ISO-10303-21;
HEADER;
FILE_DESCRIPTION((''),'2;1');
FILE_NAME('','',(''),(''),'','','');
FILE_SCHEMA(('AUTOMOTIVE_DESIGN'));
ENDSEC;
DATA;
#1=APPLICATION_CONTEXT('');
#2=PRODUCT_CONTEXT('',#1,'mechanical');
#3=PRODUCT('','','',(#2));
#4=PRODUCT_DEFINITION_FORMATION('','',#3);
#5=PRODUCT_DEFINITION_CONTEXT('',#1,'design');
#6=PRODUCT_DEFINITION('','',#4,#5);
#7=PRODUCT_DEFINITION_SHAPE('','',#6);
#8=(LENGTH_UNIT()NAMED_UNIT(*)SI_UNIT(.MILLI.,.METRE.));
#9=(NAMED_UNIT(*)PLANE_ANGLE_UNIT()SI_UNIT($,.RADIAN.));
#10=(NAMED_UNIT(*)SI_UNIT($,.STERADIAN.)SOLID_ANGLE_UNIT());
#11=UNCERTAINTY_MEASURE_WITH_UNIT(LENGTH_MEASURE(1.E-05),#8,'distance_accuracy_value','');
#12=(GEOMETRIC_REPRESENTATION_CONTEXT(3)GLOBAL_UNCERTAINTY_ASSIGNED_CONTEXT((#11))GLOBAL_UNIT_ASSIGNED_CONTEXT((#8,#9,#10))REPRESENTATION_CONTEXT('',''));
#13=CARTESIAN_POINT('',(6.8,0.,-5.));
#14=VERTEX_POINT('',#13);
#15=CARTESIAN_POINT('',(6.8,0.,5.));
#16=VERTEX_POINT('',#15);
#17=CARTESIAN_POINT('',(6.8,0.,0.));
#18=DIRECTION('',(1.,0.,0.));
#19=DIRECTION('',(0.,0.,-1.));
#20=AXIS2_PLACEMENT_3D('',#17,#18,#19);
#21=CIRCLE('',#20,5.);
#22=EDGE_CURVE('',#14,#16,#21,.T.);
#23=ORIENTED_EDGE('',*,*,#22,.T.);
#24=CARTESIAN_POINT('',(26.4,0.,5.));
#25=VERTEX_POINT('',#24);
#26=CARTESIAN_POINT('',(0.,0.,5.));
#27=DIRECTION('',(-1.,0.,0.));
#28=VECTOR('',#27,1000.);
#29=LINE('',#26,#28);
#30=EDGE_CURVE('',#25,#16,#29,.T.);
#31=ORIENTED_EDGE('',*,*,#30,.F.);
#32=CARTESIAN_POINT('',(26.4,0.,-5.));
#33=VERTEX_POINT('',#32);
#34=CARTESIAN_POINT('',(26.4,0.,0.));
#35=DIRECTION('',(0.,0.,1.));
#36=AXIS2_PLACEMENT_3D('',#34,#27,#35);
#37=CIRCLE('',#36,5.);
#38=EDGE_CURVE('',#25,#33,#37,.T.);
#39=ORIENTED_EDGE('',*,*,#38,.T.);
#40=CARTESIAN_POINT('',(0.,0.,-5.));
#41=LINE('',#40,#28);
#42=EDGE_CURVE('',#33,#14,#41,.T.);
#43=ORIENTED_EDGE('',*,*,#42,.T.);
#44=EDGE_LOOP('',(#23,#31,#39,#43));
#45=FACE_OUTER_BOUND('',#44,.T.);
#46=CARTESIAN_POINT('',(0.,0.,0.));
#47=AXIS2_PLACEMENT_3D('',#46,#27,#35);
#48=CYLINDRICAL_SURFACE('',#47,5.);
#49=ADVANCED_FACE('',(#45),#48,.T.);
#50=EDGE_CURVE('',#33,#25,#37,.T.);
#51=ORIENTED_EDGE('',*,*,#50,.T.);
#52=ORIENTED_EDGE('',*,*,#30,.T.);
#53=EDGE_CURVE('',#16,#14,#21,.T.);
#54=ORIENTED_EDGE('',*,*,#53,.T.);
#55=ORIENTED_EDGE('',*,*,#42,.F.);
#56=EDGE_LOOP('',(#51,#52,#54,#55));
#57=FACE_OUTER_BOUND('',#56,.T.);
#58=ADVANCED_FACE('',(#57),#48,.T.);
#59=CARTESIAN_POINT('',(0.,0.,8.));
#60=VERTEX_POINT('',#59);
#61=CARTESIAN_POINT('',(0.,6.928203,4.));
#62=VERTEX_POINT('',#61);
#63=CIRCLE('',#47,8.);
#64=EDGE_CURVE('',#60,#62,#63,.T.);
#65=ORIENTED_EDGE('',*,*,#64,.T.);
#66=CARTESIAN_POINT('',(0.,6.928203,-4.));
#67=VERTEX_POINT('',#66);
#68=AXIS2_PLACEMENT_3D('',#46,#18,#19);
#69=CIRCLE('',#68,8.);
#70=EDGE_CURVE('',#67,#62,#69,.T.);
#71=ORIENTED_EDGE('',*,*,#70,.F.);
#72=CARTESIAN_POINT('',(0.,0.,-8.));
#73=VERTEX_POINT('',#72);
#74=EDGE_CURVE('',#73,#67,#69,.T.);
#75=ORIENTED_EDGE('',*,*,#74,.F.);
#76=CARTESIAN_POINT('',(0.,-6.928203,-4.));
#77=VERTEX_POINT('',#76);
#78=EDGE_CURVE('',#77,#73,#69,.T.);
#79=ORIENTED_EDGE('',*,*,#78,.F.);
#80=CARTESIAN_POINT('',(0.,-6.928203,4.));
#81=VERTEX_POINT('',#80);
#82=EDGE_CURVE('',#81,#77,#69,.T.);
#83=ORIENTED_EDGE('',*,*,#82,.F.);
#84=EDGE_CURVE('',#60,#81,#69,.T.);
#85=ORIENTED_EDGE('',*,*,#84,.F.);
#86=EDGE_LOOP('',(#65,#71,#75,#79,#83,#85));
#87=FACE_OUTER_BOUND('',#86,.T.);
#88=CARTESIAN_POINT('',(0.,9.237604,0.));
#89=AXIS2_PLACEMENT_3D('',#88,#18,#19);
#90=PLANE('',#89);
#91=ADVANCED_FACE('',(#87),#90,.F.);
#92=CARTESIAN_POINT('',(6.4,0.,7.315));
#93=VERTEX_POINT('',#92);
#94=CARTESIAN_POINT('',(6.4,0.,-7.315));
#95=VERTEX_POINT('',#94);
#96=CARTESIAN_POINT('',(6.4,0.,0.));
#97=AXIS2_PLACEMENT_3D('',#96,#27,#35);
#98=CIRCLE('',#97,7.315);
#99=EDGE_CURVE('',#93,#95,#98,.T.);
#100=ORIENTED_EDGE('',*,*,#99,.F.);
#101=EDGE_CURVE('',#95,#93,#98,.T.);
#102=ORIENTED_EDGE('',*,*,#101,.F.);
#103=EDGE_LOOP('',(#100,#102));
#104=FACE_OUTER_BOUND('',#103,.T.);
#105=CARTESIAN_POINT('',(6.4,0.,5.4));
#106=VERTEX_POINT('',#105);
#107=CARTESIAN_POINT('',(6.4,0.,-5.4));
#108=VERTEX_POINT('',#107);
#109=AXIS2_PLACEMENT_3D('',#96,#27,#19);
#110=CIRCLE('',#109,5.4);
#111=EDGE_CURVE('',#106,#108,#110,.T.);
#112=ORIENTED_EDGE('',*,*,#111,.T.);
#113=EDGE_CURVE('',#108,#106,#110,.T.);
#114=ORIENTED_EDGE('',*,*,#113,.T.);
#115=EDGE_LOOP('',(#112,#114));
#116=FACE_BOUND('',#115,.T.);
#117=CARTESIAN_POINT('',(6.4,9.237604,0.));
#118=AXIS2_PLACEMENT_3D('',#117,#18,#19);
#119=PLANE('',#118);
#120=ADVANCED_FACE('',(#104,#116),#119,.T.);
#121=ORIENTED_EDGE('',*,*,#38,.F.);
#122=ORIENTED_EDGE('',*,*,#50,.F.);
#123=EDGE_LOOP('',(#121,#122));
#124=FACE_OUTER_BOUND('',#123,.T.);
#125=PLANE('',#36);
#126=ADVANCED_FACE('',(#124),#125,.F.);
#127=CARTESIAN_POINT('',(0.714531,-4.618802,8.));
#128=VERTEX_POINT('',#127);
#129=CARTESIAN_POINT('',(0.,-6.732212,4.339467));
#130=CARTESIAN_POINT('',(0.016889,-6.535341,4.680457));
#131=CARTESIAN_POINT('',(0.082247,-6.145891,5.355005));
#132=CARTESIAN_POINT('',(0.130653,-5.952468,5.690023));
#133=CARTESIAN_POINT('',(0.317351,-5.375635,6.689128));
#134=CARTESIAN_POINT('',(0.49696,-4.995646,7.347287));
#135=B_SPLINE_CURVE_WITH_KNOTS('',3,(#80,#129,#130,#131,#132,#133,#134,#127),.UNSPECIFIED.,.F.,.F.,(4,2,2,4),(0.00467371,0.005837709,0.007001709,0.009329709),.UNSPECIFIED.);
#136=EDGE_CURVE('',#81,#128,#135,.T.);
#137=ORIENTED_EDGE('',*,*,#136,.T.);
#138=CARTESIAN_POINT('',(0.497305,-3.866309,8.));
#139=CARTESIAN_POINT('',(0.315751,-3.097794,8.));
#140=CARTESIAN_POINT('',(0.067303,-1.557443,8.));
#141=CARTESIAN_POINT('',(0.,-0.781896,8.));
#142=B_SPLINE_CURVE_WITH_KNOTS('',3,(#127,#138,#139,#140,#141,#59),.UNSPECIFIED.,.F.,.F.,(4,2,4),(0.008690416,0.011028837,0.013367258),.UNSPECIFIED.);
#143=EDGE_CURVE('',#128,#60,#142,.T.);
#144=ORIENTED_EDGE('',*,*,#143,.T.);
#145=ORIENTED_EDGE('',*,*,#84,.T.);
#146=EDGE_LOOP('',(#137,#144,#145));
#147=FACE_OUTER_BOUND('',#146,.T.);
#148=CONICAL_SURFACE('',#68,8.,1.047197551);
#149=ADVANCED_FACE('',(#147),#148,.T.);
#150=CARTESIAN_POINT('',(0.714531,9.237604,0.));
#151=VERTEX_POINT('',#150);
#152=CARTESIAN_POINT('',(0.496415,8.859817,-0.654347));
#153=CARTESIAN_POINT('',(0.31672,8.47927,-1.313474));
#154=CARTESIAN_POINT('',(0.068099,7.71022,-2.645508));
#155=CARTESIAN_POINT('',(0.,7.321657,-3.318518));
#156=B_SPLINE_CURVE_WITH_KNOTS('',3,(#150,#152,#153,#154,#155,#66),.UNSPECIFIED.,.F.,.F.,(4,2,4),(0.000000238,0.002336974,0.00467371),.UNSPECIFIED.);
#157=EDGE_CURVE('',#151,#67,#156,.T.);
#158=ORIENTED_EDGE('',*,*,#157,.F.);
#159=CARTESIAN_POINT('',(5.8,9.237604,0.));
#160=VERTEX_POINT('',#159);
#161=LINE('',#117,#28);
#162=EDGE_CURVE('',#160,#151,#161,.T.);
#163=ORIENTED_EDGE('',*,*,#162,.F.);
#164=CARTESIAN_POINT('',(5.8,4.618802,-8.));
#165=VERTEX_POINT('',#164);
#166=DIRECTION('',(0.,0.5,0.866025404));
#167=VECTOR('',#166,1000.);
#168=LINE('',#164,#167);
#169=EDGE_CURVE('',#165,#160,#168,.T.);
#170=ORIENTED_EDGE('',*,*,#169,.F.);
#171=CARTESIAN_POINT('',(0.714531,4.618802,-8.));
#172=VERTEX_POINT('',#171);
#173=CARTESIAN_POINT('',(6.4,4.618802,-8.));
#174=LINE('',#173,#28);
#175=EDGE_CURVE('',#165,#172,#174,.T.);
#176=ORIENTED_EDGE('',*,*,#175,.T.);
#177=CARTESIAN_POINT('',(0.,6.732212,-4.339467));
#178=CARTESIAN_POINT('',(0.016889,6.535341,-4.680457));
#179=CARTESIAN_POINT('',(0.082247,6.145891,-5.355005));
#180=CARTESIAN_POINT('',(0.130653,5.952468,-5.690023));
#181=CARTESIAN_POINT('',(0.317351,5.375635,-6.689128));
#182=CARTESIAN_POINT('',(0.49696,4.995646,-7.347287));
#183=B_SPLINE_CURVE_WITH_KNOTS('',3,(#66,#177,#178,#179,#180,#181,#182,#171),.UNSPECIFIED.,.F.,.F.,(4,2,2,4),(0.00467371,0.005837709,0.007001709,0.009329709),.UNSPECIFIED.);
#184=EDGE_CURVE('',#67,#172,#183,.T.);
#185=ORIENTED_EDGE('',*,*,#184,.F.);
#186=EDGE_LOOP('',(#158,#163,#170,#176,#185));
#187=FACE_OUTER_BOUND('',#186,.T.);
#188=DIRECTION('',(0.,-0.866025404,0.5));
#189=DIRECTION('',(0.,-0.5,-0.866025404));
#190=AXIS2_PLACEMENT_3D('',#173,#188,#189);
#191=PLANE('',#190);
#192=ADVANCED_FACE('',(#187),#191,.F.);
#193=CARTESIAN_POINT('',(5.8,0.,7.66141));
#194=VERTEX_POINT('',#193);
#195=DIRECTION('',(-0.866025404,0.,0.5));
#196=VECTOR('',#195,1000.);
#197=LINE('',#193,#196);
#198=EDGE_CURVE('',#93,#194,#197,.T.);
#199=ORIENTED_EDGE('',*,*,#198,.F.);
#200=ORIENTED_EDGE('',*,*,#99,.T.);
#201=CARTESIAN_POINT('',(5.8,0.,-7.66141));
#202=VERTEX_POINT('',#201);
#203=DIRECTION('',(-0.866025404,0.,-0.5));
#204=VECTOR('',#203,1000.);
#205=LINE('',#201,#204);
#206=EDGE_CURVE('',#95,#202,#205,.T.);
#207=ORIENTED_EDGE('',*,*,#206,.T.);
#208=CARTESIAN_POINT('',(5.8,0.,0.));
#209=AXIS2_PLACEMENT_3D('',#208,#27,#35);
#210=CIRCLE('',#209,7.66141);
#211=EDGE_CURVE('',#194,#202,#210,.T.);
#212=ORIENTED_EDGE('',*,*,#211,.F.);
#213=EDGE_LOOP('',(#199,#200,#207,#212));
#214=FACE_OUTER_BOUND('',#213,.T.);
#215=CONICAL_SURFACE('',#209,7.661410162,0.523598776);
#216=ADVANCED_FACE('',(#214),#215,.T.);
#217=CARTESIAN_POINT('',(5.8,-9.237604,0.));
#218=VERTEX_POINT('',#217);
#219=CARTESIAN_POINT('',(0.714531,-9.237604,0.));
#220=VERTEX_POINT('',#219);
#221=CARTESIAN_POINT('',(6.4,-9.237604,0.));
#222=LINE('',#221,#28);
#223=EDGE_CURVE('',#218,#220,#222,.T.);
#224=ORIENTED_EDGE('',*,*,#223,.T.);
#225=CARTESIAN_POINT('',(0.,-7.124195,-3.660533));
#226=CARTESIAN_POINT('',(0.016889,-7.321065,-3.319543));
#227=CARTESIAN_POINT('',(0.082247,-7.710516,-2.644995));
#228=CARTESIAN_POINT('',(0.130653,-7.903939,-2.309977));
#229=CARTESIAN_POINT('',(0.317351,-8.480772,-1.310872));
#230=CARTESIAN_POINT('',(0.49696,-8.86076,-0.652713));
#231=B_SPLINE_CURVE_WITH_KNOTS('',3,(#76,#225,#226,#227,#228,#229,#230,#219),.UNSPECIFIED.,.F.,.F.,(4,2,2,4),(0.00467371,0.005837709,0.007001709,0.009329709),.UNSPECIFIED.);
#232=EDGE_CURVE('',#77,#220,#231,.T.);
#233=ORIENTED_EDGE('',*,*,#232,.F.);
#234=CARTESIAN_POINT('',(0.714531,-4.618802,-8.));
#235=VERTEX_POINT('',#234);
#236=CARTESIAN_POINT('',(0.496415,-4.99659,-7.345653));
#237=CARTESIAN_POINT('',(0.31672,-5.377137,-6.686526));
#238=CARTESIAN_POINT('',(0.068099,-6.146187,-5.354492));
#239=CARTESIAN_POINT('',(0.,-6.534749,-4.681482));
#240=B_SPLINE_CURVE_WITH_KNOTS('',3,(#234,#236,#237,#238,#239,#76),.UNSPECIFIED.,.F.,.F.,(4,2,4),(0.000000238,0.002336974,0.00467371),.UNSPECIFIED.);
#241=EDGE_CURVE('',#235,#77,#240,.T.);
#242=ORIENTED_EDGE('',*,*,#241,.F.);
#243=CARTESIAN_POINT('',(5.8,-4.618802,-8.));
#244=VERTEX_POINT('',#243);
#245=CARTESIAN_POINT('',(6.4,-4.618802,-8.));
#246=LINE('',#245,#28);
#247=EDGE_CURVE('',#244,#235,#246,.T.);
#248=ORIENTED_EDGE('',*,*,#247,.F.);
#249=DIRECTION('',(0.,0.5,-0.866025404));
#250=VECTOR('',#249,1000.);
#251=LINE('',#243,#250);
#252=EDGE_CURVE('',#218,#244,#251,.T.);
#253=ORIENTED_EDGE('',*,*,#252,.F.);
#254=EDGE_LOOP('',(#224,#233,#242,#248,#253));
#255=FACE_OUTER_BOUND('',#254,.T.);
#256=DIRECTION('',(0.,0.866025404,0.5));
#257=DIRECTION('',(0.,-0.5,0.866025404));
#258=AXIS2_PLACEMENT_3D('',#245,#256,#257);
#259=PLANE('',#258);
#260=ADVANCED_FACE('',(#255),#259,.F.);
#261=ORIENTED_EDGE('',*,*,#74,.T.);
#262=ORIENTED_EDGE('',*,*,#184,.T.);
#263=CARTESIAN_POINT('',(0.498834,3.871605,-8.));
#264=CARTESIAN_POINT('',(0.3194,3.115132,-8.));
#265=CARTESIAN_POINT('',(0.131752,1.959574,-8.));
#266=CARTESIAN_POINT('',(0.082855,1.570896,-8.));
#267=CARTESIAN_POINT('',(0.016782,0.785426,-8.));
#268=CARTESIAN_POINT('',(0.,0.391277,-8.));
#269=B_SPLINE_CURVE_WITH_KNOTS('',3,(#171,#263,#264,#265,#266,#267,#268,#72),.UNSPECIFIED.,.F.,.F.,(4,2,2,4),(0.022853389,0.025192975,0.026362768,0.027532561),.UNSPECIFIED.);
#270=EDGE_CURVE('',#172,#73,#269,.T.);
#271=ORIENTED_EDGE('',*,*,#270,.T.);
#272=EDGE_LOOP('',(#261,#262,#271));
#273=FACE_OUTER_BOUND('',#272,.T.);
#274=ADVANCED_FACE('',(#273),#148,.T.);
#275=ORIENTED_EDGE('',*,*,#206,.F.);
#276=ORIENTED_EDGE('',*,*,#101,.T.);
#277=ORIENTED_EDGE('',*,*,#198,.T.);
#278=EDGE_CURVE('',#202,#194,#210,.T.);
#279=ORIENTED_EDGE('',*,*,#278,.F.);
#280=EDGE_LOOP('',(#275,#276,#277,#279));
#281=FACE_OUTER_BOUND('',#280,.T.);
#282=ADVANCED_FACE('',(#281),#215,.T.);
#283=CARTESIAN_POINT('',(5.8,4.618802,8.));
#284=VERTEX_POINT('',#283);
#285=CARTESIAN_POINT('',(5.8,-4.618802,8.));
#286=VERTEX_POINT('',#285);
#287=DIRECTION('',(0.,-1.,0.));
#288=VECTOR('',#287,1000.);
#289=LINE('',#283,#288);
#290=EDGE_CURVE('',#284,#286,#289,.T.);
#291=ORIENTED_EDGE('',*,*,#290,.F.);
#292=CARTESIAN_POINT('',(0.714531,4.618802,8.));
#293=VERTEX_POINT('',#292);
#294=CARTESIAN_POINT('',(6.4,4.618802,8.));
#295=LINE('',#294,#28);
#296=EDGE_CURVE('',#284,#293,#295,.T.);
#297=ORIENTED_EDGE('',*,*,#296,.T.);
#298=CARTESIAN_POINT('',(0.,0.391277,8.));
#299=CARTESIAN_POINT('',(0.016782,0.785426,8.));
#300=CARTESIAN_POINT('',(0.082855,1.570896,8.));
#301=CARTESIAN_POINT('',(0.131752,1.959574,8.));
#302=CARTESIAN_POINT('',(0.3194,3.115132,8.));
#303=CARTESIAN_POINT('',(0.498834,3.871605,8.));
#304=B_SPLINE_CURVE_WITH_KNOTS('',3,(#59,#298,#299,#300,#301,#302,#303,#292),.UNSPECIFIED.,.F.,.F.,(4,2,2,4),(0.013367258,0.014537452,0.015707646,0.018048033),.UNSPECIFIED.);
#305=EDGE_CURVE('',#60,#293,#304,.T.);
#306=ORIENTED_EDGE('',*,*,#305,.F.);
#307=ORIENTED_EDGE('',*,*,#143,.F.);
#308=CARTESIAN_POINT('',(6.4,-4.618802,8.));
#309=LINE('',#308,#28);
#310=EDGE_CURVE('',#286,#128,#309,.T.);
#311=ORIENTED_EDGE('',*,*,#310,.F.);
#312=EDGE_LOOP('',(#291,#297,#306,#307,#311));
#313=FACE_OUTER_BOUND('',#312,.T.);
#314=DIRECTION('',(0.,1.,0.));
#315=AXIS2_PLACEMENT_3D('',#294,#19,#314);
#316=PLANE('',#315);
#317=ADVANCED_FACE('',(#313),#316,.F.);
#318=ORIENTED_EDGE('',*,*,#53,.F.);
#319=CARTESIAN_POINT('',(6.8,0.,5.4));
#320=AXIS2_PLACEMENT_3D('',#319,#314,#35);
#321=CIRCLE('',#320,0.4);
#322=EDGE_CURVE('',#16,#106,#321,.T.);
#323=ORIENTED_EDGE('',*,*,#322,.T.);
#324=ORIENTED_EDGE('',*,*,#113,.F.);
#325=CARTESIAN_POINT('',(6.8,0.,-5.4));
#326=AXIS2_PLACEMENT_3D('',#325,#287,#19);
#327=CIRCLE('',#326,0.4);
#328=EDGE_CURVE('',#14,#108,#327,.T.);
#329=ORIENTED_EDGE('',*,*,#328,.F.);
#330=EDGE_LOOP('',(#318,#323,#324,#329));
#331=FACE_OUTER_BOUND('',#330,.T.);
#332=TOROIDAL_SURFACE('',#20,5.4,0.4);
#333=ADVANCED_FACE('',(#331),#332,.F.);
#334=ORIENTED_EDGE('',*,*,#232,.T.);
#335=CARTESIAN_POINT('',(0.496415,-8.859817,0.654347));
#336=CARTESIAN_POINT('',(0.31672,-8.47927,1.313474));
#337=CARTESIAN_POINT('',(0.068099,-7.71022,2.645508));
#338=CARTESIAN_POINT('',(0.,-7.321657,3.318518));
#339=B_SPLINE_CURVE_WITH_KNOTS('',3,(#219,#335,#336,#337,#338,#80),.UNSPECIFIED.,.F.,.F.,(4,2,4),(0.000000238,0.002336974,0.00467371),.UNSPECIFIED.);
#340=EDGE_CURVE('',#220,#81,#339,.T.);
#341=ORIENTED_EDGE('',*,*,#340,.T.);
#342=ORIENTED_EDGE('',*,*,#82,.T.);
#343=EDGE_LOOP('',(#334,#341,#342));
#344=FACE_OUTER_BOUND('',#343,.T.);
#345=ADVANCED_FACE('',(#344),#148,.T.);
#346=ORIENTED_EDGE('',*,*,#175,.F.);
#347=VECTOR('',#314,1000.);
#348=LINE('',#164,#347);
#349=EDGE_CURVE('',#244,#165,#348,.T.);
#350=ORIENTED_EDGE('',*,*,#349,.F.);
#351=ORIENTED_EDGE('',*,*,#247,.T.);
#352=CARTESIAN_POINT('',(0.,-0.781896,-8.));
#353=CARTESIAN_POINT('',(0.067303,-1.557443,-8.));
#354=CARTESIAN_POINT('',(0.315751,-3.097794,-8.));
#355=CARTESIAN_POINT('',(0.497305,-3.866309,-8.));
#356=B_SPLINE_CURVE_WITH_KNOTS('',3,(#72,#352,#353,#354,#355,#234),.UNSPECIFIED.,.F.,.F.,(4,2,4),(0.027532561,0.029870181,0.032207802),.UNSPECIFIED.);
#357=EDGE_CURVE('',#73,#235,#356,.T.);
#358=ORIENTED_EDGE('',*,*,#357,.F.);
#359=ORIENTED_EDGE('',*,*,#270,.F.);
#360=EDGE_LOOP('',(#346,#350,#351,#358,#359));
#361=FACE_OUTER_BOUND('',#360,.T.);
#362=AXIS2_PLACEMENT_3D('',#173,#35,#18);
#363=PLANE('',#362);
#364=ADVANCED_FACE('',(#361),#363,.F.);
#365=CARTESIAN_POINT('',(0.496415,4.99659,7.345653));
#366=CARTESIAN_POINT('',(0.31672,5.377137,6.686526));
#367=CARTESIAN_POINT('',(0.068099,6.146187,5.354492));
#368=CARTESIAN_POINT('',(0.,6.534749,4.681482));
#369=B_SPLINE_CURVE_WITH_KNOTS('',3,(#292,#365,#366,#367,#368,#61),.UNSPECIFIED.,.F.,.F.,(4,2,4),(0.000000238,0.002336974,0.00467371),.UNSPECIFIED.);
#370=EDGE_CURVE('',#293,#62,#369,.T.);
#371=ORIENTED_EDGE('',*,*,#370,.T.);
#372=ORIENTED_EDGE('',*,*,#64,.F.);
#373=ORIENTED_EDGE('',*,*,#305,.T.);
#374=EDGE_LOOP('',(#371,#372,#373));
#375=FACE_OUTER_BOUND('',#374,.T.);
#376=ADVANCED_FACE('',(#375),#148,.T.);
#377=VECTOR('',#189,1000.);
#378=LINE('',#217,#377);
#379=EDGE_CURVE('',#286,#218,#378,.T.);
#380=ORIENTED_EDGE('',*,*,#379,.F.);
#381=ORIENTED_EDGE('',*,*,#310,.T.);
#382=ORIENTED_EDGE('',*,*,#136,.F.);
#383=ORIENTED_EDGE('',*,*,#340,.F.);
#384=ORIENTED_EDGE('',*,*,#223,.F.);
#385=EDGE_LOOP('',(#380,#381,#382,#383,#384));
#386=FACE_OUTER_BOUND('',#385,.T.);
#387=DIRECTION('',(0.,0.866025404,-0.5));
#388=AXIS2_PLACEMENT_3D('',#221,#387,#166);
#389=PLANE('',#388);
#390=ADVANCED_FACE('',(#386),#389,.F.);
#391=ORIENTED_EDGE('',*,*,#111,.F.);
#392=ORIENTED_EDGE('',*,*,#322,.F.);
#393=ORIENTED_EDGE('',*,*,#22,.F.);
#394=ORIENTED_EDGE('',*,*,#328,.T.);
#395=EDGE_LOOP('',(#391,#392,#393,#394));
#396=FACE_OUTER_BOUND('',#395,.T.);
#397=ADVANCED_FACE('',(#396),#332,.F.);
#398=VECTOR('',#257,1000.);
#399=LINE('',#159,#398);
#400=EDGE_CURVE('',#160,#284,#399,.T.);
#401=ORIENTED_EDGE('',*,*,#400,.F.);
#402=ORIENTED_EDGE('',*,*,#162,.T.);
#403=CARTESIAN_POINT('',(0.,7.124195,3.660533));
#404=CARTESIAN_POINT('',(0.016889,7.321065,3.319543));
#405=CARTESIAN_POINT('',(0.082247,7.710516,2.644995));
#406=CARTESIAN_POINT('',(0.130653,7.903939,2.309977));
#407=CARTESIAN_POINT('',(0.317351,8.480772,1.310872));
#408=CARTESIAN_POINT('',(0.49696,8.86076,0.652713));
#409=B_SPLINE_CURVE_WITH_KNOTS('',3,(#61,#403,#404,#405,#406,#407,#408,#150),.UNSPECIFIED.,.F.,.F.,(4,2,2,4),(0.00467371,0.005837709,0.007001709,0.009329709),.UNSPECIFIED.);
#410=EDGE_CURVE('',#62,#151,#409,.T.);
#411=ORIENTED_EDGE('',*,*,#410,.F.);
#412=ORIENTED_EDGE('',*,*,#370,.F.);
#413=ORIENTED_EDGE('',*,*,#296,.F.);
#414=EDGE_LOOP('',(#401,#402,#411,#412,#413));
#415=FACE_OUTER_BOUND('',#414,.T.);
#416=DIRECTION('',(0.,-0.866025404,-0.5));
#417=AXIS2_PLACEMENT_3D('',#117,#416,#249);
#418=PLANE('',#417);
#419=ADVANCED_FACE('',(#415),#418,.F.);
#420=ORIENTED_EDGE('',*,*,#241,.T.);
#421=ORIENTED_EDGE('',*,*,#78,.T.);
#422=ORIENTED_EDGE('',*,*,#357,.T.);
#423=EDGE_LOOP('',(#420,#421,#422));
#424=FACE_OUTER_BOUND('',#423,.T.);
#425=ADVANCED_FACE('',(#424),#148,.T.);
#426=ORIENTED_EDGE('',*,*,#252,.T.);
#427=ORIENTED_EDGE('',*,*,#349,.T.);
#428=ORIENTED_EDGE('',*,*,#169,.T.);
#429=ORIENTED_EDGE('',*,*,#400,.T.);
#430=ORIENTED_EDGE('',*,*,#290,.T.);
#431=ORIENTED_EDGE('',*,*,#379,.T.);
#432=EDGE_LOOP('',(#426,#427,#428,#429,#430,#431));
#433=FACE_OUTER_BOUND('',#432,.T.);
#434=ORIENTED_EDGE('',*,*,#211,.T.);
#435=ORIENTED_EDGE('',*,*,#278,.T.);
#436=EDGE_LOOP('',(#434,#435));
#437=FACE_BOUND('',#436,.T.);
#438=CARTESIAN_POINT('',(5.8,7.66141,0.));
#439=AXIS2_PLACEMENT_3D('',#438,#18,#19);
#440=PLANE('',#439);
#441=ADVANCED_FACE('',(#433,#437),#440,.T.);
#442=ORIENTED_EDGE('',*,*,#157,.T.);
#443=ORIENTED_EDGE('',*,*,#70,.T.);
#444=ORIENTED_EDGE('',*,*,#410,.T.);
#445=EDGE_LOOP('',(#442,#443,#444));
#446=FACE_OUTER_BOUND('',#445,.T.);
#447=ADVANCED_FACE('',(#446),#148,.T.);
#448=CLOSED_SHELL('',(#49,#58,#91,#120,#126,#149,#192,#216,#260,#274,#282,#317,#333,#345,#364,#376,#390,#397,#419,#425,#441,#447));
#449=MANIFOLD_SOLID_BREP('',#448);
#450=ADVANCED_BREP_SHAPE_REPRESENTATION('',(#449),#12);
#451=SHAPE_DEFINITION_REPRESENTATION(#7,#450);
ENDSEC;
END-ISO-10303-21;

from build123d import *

# Parameters (mm, degrees)
EXTRUDE_387_DEPTH = 6.4
FILLET_1310_R     = 0.4


with BuildPart() as part:
    # 草图1 → Extrude 387 (new body)
    with BuildSketch(Plane(origin=(0, 0, 0), x_dir=(0, 0, -1), z_dir=(1, 0, 0))):
        Polygon((8, 4.618802154), (8, -4.618802154), (0, -9.237604307), (-8, -4.618802154), (-8, 4.618802154), (0, 9.237604307), align=None)
    extrude(amount=EXTRUDE_387_DEPTH)

    # 草图2 → 凸台-旋转1 (revolve)
    with BuildSketch(Plane.XY, mode=Mode.PRIVATE) as revolve_1_sk:
        Polygon((0, 0), (26.4, 0), (26.4, 3.701), (26.4, 5), (11.4, 5), (0, 5), align=None)
    revolve(revolve_1_sk.sketch.rotate(Axis((0, 0, 0), (1, 0, 0)), 90), axis=Axis((0, 0, 0), (1, 0, 0)))

    # 草图3 → 切除-旋转1 (revolve, cut)
    with BuildSketch(Plane.XY):
        Polygon((0, 8), (3.601282526, 14.237604307), (3.601282526, 19.237604307), (-10, 19.237604307), (-10, 8), align=None)
    revolve(axis=Axis((0, 0, 0), (1, 0, 0)), mode=Mode.SUBTRACT)

    # 草图4 → 切除-旋转3 (revolve, cut)
    with BuildSketch(Plane.XY, mode=Mode.PRIVATE) as cut_revolve_3_sk:
        Polygon((6.4, 7.315), (5.8, 7.661410162), (5.8, 9.237604307), (6.4, 9.237604307), align=None)
    revolve(cut_revolve_3_sk.sketch.rotate(Axis((0, 0, 0), (1, 0, 0)), 90), axis=Axis((0, 0, 0), (1, 0, 0)), mode=Mode.SUBTRACT)

    # Fillet 1310
    fillet_1310_edges = [part.edges().sort_by_distance(p)[0] for p in [
        (6.4, 0, -5),
    ]]
    fillet(fillet_1310_edges, radius=FILLET_1310_R)


solid = part.part
